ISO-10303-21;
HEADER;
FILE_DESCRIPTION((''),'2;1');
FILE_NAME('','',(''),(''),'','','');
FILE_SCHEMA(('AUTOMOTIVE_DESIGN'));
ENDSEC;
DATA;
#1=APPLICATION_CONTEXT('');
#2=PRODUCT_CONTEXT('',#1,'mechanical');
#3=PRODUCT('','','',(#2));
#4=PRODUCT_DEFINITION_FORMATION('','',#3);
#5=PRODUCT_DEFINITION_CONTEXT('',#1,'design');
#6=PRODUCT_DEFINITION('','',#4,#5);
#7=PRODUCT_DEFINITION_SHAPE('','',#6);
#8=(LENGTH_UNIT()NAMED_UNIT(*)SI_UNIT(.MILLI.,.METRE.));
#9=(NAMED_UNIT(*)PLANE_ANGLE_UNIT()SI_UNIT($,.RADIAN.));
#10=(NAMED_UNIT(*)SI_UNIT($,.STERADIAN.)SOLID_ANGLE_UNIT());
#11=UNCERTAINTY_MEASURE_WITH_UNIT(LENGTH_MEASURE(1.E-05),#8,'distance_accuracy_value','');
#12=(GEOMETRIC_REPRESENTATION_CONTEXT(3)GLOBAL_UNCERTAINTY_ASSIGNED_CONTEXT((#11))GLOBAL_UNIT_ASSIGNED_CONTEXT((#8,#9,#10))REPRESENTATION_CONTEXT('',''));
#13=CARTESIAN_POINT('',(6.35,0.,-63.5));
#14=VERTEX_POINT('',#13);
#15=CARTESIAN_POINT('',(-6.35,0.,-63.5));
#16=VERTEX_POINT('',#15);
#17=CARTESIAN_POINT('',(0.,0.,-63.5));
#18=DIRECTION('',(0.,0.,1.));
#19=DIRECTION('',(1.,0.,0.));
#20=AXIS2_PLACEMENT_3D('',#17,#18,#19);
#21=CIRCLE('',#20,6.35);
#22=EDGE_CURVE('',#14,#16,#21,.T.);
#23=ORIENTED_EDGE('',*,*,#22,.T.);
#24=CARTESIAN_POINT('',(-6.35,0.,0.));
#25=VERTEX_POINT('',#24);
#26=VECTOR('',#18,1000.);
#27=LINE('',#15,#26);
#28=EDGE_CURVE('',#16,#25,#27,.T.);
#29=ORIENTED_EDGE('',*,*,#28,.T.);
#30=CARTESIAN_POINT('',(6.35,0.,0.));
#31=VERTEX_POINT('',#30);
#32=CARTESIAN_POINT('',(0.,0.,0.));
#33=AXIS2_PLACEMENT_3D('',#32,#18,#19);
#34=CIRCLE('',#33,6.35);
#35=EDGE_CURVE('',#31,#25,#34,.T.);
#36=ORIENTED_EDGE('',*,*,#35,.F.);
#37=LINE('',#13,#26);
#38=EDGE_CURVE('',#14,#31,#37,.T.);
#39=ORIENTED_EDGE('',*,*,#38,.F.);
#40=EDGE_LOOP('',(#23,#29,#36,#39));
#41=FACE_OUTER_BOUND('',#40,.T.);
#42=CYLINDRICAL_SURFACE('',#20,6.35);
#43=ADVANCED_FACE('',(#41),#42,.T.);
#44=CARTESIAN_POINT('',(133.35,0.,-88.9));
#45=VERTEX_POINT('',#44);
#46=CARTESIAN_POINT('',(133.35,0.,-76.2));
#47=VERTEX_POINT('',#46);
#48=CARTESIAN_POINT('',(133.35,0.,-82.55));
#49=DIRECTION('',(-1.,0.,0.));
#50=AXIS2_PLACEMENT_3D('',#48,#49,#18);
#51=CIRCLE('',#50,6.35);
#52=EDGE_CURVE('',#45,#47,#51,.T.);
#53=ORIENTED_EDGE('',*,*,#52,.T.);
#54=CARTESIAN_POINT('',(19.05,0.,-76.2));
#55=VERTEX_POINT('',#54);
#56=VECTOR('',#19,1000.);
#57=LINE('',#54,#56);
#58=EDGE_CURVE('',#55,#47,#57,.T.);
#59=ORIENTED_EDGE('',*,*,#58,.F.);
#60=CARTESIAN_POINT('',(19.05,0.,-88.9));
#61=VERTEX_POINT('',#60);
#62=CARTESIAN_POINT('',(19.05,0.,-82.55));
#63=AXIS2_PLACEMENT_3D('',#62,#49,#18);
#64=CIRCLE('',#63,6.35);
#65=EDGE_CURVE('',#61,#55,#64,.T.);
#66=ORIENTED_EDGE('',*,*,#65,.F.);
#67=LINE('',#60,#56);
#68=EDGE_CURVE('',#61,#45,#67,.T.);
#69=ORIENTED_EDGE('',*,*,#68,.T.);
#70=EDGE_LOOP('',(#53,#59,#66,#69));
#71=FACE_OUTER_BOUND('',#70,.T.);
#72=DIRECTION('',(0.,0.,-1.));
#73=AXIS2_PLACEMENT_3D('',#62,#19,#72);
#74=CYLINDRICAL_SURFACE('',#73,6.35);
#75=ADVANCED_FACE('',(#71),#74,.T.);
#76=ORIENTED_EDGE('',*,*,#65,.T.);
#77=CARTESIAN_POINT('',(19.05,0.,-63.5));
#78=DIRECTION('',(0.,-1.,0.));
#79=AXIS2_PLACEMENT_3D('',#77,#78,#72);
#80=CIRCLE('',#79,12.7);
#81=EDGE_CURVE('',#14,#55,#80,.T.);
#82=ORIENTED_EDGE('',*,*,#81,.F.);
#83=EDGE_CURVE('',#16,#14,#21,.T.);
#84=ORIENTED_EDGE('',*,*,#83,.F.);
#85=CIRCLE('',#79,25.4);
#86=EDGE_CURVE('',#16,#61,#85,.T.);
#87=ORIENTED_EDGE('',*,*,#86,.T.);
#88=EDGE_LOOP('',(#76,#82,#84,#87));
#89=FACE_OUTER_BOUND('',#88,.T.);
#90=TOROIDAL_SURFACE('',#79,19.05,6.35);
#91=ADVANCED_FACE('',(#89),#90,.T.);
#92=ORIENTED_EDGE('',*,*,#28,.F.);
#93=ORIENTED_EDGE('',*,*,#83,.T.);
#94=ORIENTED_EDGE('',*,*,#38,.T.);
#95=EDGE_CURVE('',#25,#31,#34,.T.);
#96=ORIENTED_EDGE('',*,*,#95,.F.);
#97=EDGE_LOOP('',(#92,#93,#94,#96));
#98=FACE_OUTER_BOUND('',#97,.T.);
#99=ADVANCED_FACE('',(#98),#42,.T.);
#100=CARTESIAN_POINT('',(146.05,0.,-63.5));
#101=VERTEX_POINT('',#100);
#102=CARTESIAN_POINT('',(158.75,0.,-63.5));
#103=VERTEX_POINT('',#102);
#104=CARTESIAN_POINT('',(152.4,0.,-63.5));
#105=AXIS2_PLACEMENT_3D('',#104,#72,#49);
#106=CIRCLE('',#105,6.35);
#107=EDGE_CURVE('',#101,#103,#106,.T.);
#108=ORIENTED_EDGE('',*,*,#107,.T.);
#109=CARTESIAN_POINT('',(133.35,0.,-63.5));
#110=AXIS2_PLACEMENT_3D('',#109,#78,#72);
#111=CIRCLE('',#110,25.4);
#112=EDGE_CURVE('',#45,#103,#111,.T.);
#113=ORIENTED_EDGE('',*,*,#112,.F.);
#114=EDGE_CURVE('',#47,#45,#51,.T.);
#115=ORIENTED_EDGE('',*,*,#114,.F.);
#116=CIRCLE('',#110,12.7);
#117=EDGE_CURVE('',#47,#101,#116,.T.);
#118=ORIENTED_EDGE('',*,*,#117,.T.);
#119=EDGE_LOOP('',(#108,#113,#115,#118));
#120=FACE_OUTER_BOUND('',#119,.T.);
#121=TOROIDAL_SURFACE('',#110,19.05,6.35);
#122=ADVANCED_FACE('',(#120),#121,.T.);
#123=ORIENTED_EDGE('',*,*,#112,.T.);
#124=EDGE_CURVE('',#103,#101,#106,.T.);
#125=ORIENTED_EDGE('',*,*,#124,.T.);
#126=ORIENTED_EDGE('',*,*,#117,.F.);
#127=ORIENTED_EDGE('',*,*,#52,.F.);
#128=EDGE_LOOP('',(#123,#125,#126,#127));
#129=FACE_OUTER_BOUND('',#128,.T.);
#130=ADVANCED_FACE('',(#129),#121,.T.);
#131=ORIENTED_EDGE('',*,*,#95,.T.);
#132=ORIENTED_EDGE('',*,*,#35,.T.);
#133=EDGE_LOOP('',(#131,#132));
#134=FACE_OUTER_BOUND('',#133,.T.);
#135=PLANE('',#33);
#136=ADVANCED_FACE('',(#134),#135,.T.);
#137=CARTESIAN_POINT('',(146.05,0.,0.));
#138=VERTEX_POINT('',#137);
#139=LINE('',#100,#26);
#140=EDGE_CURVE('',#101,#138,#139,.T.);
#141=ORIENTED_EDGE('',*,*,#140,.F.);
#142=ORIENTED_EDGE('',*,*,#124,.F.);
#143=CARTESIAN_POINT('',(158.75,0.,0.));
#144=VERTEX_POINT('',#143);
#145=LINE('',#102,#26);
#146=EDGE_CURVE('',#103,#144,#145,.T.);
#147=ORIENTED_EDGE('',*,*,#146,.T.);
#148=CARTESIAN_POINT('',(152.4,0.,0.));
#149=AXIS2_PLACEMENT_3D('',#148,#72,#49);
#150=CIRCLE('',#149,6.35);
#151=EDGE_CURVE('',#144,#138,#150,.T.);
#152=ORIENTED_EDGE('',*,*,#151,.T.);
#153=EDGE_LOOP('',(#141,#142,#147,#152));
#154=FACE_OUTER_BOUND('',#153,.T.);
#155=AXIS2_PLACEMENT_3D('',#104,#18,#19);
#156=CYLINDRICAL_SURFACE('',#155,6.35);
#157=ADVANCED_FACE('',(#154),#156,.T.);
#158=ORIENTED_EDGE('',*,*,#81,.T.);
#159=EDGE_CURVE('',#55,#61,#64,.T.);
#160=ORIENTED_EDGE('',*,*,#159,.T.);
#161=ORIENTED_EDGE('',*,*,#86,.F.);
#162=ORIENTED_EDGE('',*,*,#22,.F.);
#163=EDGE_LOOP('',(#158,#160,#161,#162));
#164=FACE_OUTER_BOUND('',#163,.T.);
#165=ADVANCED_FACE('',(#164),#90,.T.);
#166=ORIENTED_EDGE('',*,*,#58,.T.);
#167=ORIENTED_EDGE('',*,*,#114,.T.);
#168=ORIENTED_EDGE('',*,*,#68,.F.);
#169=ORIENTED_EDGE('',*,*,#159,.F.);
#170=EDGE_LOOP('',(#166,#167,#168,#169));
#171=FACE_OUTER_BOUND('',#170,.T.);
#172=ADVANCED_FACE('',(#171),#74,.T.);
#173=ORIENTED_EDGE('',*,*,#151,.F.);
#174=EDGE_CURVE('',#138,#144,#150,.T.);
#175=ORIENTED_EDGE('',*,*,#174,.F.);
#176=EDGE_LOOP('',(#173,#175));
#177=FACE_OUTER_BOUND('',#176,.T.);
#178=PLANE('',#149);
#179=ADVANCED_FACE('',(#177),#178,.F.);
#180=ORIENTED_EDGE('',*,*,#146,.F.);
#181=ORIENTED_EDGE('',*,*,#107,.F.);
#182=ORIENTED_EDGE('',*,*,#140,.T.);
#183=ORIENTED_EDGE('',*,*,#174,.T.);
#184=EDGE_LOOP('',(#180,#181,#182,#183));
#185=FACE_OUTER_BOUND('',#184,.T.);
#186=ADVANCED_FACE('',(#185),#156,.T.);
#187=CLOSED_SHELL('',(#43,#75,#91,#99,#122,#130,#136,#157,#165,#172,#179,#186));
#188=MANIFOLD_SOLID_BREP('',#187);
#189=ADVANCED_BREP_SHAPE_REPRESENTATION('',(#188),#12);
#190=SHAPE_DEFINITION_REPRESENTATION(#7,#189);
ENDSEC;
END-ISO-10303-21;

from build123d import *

# Parameters (mm, degrees)
SKETCH1_R = 6.35


with BuildPart() as part:
    # Sweep1: sweep along a path in Sketch2
    with BuildLine(Plane(origin=(0, 0, 0), x_dir=(1, 0, 0), z_dir=(0, 1, 0))) as sweep1_path:
        Line((0, 0), (0, 63.5))
        ThreePointArc((0, 63.5), (5.579615818, 76.970384182), (19.05, 82.55))
        Line((19.05, 82.55), (133.35, 82.55))
        ThreePointArc((133.35, 82.55), (146.820384182, 76.970384182), (152.4, 63.5))
        Line((152.4, 63.5), (152.4, 0))
    # Sketch1 → Sweep1 (sweep)
    with BuildSketch(Plane.XY):
        Circle(SKETCH1_R)
    sweep(path=sweep1_path.line)


solid = part.part
